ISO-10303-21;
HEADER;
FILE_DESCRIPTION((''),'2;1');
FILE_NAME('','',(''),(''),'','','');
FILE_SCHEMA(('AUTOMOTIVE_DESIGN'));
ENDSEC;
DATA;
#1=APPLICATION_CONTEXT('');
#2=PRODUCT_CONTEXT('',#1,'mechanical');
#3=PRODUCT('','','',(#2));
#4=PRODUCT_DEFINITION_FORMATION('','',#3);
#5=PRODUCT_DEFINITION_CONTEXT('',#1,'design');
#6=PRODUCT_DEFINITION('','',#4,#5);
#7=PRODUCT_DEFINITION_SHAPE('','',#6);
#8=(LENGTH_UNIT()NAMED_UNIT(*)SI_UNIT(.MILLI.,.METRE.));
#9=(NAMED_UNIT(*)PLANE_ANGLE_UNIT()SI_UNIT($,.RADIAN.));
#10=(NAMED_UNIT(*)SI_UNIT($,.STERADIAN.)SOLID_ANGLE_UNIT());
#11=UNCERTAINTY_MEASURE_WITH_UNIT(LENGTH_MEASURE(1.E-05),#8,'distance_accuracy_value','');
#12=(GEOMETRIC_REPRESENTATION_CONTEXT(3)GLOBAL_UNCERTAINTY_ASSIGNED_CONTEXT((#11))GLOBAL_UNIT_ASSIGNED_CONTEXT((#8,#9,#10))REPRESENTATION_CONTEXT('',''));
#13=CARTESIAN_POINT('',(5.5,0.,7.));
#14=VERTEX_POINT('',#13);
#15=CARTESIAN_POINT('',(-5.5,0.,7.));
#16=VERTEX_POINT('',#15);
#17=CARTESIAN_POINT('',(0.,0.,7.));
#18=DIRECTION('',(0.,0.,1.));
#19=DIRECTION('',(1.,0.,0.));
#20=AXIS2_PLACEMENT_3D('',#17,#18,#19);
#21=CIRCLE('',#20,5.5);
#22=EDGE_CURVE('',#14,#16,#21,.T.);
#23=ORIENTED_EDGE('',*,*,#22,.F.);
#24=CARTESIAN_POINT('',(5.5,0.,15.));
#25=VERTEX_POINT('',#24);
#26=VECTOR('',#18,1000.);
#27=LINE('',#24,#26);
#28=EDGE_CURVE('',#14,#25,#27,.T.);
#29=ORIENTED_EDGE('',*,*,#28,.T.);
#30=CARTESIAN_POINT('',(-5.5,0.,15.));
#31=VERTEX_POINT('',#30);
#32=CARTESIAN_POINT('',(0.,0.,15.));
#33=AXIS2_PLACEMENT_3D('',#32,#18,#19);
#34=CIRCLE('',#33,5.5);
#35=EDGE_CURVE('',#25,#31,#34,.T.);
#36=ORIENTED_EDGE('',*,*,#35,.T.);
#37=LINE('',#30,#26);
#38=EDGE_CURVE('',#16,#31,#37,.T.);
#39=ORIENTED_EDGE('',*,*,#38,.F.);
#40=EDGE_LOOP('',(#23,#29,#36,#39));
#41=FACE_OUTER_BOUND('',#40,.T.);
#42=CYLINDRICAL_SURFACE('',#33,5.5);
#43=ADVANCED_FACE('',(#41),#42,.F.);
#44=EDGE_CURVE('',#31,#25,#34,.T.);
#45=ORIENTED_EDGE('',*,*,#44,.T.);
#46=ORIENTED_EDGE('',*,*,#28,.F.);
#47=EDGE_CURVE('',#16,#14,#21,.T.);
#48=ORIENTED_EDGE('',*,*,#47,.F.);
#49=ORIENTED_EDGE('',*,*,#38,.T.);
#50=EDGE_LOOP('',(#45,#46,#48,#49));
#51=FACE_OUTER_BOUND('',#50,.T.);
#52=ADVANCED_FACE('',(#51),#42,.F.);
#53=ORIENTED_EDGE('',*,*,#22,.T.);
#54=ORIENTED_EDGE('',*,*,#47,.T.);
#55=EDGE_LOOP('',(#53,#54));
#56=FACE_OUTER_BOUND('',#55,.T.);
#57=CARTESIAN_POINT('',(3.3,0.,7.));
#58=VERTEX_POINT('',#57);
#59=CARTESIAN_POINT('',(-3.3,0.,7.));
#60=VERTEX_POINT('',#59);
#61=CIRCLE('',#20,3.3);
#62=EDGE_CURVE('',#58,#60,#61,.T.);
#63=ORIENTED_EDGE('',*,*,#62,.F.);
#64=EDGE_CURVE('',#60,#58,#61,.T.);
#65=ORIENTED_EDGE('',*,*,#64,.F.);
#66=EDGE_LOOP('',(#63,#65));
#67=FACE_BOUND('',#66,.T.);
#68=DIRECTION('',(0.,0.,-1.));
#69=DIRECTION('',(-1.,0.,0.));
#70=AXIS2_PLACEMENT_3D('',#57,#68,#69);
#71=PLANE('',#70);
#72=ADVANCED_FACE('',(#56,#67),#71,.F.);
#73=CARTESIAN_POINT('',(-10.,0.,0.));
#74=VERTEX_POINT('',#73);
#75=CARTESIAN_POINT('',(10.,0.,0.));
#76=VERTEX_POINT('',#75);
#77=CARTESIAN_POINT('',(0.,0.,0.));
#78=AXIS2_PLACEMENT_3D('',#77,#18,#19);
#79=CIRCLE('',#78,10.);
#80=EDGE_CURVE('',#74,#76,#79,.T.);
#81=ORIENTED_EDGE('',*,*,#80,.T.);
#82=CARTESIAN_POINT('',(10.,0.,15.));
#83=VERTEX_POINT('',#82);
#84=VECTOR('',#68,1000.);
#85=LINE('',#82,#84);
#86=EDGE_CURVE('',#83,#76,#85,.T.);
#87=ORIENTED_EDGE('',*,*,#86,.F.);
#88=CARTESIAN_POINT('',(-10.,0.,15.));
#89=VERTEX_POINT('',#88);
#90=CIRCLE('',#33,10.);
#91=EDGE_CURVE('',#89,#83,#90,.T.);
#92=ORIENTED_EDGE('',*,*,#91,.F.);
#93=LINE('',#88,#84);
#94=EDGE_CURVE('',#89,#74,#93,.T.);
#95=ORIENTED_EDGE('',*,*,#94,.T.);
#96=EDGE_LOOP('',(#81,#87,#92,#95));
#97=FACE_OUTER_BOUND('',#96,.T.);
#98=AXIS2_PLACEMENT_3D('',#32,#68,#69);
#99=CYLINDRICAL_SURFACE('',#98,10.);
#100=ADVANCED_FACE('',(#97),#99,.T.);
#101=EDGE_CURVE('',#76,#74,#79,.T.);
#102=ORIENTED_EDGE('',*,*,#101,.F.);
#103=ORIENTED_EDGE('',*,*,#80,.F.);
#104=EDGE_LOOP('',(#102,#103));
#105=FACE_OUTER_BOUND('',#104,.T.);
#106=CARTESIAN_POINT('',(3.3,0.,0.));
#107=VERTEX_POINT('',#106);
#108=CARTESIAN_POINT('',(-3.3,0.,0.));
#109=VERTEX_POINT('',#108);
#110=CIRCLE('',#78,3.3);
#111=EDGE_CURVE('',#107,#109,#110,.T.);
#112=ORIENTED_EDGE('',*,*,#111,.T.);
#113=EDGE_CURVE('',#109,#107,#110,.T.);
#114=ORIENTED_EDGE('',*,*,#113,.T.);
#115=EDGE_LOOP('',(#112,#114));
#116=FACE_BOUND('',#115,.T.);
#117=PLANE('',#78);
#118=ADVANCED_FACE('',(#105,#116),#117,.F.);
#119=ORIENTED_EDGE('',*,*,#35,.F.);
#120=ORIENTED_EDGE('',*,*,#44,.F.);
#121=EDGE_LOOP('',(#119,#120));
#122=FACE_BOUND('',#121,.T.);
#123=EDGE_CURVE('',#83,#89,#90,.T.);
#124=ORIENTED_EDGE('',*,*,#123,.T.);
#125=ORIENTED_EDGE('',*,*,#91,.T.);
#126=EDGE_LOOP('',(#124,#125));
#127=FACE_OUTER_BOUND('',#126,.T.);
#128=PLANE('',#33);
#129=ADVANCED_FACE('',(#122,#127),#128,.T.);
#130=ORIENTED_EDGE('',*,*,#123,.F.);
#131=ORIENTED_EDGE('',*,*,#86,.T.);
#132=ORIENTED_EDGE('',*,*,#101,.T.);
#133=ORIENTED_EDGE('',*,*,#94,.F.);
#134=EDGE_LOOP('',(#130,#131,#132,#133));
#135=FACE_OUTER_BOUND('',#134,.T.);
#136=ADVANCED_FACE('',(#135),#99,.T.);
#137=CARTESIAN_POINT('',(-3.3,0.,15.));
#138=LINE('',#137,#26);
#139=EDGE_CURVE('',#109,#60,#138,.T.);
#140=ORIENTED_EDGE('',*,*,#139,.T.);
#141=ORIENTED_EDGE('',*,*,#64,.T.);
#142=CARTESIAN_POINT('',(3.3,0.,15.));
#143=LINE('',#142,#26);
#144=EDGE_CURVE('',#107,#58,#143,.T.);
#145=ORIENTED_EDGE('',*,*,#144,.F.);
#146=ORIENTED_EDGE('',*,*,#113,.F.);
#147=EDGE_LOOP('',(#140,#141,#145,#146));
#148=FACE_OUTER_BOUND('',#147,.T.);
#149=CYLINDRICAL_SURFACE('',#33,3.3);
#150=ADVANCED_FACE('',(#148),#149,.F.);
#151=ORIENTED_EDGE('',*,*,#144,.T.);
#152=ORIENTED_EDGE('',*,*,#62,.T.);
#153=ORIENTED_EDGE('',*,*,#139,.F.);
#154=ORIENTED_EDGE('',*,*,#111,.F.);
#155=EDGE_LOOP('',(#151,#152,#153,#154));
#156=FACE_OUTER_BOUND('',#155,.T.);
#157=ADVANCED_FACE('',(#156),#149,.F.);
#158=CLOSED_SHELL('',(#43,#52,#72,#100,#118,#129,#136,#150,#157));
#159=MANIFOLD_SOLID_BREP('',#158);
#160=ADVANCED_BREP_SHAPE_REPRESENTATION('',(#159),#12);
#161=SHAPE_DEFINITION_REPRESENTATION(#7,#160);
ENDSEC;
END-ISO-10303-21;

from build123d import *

# Parameters (mm, degrees)
SKETCH_1_R                = 10
EXTRUDE_1_DEPTH           = 15
HOLE_WIZARD_1_D           = 6.6
HOLE_WIZARD_1_CBORE_D     = 11
HOLE_WIZARD_1_CBORE_DEPTH = 8


with BuildPart() as part:
    # 草图1 → 凸台-拉伸1 (new body)
    with BuildSketch(Plane.XY):
        Circle(SKETCH_1_R)
    extrude(amount=EXTRUDE_1_DEPTH)

    # 打孔尺寸(%根据)内六角圆柱头螺钉的类型1 (through all)
    with Locations(Plane.XY.offset(15)):
        with Locations((0, 0)):
            CounterBoreHole(HOLE_WIZARD_1_D / 2, HOLE_WIZARD_1_CBORE_D / 2, HOLE_WIZARD_1_CBORE_DEPTH)


solid = part.part
